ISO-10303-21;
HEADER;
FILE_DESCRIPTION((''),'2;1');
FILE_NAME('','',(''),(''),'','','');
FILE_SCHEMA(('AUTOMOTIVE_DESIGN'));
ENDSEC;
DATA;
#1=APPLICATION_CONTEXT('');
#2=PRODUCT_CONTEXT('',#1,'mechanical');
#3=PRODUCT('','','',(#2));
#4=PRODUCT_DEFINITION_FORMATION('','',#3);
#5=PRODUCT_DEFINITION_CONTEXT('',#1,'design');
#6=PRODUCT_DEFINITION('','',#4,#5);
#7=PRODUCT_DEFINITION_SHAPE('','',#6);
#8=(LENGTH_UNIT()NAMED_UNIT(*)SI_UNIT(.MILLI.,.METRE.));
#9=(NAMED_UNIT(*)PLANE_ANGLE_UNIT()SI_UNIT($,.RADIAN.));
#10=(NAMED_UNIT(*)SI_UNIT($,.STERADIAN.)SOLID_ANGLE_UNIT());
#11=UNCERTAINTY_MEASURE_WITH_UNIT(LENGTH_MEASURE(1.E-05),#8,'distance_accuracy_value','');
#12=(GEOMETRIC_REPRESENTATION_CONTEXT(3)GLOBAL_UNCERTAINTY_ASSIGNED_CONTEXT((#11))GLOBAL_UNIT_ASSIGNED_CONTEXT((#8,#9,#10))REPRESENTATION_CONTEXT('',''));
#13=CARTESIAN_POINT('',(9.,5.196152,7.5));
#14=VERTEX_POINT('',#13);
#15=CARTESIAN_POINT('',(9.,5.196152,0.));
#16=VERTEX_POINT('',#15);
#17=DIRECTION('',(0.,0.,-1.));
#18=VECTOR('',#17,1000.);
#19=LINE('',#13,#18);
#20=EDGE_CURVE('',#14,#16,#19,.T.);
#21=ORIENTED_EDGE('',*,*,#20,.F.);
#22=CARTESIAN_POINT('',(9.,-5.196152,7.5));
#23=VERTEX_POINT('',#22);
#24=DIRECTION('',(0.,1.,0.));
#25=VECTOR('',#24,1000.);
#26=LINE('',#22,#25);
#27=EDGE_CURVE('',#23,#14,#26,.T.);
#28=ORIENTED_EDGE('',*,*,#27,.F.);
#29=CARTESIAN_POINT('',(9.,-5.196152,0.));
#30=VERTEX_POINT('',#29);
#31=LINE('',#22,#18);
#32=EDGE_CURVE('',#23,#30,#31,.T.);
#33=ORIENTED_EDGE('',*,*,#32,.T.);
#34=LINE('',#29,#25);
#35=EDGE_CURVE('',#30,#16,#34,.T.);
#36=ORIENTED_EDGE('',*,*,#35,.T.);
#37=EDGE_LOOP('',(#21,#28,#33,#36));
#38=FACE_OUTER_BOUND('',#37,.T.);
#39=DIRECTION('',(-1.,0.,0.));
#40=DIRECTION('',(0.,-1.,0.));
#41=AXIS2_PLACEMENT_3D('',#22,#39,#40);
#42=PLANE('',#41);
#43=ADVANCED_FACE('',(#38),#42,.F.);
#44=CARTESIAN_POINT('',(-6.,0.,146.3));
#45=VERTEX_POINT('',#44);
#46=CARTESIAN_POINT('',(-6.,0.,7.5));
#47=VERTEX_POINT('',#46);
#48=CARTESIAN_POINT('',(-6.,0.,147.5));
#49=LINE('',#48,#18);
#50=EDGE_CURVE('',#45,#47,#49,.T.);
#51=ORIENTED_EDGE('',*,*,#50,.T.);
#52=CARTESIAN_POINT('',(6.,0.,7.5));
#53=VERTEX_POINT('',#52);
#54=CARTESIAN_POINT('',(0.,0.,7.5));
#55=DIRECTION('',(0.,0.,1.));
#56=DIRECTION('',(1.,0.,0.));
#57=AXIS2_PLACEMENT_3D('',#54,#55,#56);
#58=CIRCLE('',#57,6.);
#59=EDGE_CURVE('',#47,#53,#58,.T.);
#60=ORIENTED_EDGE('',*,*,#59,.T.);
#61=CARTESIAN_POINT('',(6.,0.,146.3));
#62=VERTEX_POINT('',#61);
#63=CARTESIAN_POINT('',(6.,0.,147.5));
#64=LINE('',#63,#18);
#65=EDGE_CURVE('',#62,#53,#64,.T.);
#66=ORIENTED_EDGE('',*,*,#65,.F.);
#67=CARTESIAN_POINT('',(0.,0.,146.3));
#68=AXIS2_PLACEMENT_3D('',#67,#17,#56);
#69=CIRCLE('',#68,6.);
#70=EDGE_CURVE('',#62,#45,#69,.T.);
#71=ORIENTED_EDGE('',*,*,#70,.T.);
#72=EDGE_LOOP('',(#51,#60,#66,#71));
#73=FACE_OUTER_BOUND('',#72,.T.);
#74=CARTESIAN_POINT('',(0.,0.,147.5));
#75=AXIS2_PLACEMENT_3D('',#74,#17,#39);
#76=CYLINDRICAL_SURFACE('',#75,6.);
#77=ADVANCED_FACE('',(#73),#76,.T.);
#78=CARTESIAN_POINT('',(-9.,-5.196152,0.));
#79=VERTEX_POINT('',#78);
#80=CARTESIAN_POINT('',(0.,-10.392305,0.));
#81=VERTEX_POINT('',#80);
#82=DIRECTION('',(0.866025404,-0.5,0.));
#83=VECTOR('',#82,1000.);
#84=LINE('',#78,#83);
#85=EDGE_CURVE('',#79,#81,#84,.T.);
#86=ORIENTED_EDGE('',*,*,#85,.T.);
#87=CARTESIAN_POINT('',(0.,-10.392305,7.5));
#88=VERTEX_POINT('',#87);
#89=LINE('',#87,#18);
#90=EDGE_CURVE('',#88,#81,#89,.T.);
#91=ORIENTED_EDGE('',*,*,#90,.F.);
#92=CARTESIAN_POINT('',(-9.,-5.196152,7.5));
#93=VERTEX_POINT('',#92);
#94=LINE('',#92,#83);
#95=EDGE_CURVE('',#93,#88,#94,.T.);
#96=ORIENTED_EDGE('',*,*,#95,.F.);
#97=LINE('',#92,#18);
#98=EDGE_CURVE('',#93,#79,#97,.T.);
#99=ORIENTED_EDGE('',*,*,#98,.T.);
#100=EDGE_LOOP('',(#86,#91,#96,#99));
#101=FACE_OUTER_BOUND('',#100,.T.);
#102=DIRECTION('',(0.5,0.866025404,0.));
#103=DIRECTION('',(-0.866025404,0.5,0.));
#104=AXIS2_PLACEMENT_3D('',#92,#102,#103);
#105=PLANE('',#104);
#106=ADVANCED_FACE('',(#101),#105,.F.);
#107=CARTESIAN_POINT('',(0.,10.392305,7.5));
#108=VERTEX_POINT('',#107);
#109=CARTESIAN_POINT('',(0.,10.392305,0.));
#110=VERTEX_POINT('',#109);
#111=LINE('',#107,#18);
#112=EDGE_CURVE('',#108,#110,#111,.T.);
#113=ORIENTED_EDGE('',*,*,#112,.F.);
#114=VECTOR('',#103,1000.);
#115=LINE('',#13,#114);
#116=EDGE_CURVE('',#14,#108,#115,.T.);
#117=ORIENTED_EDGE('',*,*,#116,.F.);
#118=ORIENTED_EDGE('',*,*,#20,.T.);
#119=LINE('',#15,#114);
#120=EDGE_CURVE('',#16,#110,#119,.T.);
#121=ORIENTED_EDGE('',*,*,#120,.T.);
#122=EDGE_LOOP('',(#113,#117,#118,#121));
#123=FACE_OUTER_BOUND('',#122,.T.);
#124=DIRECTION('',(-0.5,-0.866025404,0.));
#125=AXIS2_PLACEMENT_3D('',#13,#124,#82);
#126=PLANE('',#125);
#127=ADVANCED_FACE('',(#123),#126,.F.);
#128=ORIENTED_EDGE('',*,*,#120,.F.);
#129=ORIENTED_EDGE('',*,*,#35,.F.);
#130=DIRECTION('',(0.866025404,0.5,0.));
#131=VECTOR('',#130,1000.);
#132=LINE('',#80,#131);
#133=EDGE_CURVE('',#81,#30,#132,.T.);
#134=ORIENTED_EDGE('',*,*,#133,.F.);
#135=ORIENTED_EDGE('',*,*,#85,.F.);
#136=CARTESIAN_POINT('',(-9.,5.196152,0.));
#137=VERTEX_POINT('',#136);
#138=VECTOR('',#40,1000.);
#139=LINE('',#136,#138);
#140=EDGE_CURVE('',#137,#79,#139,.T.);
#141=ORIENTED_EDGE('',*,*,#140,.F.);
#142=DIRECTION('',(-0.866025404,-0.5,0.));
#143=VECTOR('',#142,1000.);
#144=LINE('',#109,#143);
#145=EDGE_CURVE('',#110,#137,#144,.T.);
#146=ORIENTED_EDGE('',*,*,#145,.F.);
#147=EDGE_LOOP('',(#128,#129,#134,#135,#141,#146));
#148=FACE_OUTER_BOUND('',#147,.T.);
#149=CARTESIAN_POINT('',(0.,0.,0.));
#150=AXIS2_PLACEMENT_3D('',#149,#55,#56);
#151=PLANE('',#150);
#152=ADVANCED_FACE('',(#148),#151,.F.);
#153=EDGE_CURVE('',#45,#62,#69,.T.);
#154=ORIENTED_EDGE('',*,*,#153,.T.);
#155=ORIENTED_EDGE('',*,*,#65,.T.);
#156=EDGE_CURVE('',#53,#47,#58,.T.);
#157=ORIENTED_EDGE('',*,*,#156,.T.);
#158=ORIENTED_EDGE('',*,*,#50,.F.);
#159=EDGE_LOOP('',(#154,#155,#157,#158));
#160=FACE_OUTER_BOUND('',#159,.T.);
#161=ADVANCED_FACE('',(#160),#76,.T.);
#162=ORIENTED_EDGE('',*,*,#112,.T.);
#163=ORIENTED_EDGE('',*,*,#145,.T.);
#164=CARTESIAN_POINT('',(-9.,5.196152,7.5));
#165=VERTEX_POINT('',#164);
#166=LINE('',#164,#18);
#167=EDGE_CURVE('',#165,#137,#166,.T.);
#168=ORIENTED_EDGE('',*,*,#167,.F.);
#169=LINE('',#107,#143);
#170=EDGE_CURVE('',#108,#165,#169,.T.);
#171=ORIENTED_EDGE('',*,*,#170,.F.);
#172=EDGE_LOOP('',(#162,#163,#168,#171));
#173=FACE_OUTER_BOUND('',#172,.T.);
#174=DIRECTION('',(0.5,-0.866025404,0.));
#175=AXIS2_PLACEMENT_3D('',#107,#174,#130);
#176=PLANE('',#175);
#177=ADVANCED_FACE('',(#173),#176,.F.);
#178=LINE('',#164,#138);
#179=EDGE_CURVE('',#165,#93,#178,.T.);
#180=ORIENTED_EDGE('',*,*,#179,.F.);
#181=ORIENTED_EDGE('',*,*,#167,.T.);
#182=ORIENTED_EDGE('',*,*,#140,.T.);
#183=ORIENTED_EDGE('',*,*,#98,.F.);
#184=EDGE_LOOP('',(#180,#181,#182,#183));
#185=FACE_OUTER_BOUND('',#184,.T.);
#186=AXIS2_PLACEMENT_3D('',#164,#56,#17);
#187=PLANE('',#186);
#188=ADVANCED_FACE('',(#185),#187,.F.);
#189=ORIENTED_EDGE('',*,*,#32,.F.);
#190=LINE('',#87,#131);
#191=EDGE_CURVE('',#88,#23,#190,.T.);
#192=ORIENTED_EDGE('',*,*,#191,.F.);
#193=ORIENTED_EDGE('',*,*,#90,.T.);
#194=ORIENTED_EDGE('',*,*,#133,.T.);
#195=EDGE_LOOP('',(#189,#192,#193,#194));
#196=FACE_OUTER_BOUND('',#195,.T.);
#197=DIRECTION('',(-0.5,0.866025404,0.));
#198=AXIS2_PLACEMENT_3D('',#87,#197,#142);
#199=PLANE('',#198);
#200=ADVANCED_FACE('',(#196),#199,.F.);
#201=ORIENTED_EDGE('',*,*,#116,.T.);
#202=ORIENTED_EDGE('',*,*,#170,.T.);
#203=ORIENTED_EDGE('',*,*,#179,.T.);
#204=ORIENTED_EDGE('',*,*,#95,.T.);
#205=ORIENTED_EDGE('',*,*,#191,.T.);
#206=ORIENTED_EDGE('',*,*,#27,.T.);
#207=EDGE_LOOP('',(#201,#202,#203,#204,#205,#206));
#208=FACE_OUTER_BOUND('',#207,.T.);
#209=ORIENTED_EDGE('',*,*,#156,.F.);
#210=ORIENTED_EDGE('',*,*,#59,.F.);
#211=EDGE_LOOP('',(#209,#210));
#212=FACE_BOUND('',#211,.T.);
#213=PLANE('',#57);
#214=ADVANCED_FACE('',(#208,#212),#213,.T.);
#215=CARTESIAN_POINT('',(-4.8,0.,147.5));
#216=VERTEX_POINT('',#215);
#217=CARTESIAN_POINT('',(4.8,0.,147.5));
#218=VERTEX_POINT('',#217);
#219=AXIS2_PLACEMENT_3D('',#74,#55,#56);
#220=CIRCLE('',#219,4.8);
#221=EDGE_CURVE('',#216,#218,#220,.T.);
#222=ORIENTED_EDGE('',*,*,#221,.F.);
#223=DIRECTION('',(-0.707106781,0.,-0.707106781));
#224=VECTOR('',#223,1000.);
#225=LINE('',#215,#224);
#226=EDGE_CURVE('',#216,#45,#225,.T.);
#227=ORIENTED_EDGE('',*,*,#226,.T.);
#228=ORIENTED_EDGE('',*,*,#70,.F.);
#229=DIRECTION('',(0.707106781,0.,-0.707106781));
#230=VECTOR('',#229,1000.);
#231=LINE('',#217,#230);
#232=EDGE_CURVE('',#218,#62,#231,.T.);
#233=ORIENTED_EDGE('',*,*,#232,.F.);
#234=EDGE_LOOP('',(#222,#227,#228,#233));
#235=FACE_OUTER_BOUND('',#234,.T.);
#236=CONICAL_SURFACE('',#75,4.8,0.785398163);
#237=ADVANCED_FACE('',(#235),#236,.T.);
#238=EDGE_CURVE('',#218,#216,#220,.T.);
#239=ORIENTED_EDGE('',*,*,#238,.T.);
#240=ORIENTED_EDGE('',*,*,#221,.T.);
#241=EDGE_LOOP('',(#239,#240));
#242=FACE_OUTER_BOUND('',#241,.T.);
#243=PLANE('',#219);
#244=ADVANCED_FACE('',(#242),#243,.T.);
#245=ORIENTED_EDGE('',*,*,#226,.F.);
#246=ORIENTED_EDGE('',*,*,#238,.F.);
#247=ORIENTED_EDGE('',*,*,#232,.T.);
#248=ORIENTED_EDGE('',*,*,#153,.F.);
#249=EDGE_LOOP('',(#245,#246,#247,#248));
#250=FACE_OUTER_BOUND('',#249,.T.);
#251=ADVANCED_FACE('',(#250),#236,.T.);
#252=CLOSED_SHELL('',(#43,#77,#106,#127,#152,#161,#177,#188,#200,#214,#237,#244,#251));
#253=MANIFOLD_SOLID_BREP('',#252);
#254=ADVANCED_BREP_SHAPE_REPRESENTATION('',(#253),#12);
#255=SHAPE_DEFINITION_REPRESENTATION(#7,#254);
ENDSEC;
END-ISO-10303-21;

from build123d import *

# Parameters (mm, degrees)
BOSS_EXTRUDE1_DEPTH = 7.5
SKETCH3_R           = 6
BOSS_EXTRUDE2_DEPTH = 140
CHAMFER1_SIZE       = 1.2


with BuildPart() as part:
    # Sketch1 → Boss-Extrude1 (new body)
    with BuildSketch(Plane.XY):
        Polygon((9, 5.196152423), (0, 10.392304845), (-9, 5.196152423), (-9, -5.196152423), (0, -10.392304845), (9, -5.196152423), align=None)
    extrude(amount=BOSS_EXTRUDE1_DEPTH)

    # Sketch3 → Boss-Extrude2 (add)
    with BuildSketch(Plane.XY.offset(7.5)):
        Circle(SKETCH3_R)
    extrude(amount=BOSS_EXTRUDE2_DEPTH)

    # Chamfer1
    chamfer1_edges = [part.edges().sort_by_distance(p)[0] for p in [
        (-6, 0, 147.5),
    ]]
    chamfer(chamfer1_edges, length=CHAMFER1_SIZE)


solid = part.part
